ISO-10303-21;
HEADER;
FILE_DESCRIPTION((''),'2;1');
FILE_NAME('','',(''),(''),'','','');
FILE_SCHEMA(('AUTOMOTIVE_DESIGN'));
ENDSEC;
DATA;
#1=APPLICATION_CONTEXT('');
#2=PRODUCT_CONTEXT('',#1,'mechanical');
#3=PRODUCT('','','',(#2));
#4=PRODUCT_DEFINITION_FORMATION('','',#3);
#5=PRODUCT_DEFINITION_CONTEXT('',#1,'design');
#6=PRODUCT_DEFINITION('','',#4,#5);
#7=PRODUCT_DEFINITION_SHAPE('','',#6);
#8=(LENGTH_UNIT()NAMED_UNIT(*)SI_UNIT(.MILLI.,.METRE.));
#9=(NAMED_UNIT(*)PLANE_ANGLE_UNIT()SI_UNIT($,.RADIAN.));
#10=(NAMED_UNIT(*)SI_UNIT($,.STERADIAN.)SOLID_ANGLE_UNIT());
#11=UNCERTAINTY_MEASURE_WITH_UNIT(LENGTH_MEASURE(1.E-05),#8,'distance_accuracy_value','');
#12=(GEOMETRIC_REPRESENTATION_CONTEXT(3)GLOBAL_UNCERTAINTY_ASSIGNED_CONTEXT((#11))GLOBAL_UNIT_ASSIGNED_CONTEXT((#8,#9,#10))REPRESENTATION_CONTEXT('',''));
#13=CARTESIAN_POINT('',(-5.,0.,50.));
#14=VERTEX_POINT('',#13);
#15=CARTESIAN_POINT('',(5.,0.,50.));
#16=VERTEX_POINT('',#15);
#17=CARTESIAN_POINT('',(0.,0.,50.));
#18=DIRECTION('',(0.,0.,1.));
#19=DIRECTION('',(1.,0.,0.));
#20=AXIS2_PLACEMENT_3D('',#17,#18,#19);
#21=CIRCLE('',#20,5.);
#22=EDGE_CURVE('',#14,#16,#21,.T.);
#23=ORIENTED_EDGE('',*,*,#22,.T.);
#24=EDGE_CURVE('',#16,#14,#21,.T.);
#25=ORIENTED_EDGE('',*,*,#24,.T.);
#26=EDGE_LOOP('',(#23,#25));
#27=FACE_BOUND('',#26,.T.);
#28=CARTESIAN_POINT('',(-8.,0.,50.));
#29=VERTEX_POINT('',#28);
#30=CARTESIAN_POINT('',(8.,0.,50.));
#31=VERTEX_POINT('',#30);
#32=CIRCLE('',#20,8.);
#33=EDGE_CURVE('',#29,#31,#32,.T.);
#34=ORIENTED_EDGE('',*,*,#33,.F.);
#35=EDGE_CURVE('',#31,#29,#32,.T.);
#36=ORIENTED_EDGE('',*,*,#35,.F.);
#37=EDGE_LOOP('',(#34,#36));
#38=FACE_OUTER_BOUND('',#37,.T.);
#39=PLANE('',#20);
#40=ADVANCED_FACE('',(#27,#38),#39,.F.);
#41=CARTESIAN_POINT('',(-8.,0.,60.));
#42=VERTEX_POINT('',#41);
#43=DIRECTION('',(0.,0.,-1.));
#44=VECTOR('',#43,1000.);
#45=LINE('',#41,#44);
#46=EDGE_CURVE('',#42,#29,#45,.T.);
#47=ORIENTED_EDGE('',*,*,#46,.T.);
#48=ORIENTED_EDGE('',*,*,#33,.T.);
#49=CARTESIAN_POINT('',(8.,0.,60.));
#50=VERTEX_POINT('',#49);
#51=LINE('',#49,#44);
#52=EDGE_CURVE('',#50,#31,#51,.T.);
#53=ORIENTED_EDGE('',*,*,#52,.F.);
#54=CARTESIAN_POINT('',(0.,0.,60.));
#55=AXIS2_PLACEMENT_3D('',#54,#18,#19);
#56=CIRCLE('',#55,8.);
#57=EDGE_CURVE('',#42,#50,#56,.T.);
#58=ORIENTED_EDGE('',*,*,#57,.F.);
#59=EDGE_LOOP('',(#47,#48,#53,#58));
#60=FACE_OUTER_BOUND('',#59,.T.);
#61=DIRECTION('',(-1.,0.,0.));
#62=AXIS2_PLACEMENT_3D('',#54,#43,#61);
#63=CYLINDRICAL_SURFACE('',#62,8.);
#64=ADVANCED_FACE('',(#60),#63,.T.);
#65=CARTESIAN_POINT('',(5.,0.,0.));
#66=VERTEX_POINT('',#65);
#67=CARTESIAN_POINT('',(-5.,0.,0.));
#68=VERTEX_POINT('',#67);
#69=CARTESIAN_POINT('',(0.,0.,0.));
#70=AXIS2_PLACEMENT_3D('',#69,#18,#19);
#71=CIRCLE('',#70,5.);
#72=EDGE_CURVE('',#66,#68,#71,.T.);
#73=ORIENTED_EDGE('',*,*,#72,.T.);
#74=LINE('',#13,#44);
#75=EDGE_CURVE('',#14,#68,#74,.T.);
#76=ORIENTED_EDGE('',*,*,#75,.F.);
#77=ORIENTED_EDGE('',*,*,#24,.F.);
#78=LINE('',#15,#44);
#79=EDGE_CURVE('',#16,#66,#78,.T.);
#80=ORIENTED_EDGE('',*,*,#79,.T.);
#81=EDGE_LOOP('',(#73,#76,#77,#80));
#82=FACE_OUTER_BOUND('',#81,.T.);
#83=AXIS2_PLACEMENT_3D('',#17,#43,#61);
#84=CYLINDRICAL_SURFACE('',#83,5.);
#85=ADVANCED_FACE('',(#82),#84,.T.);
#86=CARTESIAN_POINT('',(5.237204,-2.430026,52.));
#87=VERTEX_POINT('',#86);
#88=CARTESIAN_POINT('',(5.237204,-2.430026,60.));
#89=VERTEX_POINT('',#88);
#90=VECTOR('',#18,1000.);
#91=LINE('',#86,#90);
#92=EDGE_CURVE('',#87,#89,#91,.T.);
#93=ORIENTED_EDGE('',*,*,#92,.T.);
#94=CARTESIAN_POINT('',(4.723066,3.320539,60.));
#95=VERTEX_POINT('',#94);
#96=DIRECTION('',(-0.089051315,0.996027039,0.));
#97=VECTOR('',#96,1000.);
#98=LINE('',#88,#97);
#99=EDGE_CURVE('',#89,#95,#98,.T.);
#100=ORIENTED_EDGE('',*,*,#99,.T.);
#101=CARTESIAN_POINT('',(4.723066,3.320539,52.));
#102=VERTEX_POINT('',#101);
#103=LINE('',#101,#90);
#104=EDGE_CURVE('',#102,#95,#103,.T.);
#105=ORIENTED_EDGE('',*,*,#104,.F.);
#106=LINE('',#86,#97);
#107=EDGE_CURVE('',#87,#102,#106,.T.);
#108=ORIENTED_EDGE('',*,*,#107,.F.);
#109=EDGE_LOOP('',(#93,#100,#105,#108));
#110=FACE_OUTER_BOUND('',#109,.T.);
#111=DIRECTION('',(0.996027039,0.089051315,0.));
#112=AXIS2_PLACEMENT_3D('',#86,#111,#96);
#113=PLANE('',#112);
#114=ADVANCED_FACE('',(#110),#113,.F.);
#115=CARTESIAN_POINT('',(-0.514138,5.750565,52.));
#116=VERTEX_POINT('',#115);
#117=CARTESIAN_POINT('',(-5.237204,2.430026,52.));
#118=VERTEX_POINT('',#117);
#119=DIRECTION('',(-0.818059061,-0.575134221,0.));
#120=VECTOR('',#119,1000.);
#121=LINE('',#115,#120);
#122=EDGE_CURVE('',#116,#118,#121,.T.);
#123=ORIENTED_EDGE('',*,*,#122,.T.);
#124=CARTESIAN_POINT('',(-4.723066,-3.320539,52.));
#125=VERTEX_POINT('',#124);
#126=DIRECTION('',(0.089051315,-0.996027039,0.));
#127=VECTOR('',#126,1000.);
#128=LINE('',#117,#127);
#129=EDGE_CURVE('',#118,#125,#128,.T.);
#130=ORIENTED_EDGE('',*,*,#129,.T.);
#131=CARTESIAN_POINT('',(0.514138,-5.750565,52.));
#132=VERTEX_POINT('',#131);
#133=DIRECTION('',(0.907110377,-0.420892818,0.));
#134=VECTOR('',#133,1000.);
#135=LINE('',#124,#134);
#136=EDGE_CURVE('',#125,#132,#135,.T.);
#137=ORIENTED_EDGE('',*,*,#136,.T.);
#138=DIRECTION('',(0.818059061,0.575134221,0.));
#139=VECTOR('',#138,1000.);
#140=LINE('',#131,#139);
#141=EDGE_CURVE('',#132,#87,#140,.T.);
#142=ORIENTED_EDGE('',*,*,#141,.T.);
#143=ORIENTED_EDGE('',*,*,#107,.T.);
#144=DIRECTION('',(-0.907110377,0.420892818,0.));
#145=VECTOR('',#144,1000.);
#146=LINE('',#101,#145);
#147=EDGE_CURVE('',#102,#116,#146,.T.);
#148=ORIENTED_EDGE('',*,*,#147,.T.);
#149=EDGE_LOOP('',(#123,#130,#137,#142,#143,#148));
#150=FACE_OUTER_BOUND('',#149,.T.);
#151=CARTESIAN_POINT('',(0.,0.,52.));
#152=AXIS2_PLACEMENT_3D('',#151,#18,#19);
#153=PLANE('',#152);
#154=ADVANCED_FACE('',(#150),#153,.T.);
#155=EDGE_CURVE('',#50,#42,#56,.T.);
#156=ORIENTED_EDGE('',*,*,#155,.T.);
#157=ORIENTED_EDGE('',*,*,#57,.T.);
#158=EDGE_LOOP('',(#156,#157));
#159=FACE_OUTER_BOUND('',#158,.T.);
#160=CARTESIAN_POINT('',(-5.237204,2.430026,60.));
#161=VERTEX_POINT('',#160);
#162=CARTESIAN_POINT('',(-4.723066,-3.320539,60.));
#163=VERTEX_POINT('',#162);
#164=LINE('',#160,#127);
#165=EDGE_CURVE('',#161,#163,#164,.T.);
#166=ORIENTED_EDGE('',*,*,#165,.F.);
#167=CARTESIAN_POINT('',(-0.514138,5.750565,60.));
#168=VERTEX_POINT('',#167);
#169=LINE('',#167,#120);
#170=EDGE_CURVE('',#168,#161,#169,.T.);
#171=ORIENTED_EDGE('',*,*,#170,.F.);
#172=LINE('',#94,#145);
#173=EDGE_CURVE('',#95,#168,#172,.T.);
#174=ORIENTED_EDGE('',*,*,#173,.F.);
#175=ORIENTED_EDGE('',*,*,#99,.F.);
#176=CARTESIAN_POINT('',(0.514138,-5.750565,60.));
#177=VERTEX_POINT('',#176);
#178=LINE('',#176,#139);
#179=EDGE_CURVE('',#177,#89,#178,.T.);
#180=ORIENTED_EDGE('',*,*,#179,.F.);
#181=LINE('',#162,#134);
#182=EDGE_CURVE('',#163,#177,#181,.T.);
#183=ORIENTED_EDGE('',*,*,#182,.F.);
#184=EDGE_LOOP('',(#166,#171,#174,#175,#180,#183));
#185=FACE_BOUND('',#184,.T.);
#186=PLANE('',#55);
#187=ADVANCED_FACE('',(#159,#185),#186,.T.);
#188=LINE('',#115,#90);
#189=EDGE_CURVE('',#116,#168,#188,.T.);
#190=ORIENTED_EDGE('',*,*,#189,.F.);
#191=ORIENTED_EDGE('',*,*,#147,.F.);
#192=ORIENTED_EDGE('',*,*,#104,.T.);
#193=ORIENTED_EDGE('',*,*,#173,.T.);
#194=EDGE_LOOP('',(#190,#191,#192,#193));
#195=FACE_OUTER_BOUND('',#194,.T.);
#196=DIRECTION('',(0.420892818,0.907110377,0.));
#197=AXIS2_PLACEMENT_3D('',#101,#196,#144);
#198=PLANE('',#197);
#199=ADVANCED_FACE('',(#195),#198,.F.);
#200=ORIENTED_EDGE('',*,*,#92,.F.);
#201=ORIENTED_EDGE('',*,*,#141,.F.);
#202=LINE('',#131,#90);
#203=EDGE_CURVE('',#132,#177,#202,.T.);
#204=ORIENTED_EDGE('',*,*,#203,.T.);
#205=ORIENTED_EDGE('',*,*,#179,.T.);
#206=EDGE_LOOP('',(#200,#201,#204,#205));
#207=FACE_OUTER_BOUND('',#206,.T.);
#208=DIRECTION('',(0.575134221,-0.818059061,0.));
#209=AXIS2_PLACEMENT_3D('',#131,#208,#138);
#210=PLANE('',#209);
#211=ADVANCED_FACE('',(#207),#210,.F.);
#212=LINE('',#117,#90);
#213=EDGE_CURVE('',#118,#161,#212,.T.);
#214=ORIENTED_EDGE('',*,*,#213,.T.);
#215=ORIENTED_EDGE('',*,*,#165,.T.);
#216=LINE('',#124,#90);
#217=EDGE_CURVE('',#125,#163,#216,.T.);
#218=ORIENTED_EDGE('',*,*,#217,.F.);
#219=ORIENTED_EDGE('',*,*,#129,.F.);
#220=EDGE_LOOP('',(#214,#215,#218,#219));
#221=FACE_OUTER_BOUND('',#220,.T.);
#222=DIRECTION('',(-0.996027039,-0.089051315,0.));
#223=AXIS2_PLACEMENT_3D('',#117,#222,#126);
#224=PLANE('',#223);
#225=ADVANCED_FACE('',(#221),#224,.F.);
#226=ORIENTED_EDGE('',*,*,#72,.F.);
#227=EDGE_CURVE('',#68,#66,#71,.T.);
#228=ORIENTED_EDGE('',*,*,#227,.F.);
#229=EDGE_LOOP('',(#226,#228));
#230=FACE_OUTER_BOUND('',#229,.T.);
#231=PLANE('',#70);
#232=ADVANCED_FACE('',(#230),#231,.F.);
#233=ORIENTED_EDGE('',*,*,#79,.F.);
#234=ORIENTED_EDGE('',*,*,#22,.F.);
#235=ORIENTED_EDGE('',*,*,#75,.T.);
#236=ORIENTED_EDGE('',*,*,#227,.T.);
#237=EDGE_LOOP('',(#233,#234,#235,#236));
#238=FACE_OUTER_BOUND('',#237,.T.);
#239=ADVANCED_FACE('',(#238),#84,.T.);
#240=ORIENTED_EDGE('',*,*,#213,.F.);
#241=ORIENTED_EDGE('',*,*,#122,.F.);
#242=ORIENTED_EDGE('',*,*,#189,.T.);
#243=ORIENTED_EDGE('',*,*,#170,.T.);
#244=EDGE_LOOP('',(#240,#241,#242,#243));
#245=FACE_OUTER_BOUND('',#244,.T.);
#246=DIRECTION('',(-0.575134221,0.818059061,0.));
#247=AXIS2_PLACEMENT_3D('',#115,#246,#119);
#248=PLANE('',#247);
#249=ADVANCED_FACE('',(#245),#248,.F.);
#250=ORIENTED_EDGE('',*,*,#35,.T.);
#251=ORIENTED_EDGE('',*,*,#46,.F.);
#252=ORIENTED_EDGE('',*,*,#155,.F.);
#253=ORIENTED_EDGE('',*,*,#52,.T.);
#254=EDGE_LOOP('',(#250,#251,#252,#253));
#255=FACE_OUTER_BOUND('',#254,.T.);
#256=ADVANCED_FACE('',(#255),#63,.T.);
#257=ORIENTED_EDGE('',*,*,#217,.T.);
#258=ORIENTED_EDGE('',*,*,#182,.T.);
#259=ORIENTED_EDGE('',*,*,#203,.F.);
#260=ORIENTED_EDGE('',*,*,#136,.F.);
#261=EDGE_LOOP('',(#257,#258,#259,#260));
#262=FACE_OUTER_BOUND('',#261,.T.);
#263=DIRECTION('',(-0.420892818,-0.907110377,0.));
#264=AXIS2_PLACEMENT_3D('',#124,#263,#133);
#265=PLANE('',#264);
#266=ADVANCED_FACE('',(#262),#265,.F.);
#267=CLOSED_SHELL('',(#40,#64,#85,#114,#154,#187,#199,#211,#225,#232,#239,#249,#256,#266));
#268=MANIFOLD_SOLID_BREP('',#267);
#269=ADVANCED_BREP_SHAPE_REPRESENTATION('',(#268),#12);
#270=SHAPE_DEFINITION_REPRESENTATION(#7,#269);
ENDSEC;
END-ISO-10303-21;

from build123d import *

# Parameters (mm, degrees)
SKETCH1_R           = 5
BOSS_EXTRUDE1_DEPTH = 50
SKETCH2_R           = 8
BOSS_EXTRUDE2_DEPTH = 10
CUT_EXTRUDE1_DEPTH  = 8


with BuildPart() as part:
    # Sketch1 → Boss-Extrude1 (new body)
    with BuildSketch(Plane.XY):
        Circle(SKETCH1_R)
    extrude(amount=BOSS_EXTRUDE1_DEPTH)

    # Sketch2 → Boss-Extrude2 (add)
    with BuildSketch(Plane.XY.offset(50)):
        Circle(SKETCH2_R)
    extrude(amount=BOSS_EXTRUDE2_DEPTH)

    # Sketch3 → Cut-Extrude1 (cut)
    with BuildSketch(Plane.XY.offset(60)):
        Polygon((0.514138009, -5.750564793), (5.237204202, -2.430025819), (4.723066192, 3.320538974), (-0.514138009, 5.750564793), (-5.237204202, 2.430025819), (-4.723066192, -3.320538974), align=None)
    extrude(amount=-CUT_EXTRUDE1_DEPTH, mode=Mode.SUBTRACT)


solid = part.part
